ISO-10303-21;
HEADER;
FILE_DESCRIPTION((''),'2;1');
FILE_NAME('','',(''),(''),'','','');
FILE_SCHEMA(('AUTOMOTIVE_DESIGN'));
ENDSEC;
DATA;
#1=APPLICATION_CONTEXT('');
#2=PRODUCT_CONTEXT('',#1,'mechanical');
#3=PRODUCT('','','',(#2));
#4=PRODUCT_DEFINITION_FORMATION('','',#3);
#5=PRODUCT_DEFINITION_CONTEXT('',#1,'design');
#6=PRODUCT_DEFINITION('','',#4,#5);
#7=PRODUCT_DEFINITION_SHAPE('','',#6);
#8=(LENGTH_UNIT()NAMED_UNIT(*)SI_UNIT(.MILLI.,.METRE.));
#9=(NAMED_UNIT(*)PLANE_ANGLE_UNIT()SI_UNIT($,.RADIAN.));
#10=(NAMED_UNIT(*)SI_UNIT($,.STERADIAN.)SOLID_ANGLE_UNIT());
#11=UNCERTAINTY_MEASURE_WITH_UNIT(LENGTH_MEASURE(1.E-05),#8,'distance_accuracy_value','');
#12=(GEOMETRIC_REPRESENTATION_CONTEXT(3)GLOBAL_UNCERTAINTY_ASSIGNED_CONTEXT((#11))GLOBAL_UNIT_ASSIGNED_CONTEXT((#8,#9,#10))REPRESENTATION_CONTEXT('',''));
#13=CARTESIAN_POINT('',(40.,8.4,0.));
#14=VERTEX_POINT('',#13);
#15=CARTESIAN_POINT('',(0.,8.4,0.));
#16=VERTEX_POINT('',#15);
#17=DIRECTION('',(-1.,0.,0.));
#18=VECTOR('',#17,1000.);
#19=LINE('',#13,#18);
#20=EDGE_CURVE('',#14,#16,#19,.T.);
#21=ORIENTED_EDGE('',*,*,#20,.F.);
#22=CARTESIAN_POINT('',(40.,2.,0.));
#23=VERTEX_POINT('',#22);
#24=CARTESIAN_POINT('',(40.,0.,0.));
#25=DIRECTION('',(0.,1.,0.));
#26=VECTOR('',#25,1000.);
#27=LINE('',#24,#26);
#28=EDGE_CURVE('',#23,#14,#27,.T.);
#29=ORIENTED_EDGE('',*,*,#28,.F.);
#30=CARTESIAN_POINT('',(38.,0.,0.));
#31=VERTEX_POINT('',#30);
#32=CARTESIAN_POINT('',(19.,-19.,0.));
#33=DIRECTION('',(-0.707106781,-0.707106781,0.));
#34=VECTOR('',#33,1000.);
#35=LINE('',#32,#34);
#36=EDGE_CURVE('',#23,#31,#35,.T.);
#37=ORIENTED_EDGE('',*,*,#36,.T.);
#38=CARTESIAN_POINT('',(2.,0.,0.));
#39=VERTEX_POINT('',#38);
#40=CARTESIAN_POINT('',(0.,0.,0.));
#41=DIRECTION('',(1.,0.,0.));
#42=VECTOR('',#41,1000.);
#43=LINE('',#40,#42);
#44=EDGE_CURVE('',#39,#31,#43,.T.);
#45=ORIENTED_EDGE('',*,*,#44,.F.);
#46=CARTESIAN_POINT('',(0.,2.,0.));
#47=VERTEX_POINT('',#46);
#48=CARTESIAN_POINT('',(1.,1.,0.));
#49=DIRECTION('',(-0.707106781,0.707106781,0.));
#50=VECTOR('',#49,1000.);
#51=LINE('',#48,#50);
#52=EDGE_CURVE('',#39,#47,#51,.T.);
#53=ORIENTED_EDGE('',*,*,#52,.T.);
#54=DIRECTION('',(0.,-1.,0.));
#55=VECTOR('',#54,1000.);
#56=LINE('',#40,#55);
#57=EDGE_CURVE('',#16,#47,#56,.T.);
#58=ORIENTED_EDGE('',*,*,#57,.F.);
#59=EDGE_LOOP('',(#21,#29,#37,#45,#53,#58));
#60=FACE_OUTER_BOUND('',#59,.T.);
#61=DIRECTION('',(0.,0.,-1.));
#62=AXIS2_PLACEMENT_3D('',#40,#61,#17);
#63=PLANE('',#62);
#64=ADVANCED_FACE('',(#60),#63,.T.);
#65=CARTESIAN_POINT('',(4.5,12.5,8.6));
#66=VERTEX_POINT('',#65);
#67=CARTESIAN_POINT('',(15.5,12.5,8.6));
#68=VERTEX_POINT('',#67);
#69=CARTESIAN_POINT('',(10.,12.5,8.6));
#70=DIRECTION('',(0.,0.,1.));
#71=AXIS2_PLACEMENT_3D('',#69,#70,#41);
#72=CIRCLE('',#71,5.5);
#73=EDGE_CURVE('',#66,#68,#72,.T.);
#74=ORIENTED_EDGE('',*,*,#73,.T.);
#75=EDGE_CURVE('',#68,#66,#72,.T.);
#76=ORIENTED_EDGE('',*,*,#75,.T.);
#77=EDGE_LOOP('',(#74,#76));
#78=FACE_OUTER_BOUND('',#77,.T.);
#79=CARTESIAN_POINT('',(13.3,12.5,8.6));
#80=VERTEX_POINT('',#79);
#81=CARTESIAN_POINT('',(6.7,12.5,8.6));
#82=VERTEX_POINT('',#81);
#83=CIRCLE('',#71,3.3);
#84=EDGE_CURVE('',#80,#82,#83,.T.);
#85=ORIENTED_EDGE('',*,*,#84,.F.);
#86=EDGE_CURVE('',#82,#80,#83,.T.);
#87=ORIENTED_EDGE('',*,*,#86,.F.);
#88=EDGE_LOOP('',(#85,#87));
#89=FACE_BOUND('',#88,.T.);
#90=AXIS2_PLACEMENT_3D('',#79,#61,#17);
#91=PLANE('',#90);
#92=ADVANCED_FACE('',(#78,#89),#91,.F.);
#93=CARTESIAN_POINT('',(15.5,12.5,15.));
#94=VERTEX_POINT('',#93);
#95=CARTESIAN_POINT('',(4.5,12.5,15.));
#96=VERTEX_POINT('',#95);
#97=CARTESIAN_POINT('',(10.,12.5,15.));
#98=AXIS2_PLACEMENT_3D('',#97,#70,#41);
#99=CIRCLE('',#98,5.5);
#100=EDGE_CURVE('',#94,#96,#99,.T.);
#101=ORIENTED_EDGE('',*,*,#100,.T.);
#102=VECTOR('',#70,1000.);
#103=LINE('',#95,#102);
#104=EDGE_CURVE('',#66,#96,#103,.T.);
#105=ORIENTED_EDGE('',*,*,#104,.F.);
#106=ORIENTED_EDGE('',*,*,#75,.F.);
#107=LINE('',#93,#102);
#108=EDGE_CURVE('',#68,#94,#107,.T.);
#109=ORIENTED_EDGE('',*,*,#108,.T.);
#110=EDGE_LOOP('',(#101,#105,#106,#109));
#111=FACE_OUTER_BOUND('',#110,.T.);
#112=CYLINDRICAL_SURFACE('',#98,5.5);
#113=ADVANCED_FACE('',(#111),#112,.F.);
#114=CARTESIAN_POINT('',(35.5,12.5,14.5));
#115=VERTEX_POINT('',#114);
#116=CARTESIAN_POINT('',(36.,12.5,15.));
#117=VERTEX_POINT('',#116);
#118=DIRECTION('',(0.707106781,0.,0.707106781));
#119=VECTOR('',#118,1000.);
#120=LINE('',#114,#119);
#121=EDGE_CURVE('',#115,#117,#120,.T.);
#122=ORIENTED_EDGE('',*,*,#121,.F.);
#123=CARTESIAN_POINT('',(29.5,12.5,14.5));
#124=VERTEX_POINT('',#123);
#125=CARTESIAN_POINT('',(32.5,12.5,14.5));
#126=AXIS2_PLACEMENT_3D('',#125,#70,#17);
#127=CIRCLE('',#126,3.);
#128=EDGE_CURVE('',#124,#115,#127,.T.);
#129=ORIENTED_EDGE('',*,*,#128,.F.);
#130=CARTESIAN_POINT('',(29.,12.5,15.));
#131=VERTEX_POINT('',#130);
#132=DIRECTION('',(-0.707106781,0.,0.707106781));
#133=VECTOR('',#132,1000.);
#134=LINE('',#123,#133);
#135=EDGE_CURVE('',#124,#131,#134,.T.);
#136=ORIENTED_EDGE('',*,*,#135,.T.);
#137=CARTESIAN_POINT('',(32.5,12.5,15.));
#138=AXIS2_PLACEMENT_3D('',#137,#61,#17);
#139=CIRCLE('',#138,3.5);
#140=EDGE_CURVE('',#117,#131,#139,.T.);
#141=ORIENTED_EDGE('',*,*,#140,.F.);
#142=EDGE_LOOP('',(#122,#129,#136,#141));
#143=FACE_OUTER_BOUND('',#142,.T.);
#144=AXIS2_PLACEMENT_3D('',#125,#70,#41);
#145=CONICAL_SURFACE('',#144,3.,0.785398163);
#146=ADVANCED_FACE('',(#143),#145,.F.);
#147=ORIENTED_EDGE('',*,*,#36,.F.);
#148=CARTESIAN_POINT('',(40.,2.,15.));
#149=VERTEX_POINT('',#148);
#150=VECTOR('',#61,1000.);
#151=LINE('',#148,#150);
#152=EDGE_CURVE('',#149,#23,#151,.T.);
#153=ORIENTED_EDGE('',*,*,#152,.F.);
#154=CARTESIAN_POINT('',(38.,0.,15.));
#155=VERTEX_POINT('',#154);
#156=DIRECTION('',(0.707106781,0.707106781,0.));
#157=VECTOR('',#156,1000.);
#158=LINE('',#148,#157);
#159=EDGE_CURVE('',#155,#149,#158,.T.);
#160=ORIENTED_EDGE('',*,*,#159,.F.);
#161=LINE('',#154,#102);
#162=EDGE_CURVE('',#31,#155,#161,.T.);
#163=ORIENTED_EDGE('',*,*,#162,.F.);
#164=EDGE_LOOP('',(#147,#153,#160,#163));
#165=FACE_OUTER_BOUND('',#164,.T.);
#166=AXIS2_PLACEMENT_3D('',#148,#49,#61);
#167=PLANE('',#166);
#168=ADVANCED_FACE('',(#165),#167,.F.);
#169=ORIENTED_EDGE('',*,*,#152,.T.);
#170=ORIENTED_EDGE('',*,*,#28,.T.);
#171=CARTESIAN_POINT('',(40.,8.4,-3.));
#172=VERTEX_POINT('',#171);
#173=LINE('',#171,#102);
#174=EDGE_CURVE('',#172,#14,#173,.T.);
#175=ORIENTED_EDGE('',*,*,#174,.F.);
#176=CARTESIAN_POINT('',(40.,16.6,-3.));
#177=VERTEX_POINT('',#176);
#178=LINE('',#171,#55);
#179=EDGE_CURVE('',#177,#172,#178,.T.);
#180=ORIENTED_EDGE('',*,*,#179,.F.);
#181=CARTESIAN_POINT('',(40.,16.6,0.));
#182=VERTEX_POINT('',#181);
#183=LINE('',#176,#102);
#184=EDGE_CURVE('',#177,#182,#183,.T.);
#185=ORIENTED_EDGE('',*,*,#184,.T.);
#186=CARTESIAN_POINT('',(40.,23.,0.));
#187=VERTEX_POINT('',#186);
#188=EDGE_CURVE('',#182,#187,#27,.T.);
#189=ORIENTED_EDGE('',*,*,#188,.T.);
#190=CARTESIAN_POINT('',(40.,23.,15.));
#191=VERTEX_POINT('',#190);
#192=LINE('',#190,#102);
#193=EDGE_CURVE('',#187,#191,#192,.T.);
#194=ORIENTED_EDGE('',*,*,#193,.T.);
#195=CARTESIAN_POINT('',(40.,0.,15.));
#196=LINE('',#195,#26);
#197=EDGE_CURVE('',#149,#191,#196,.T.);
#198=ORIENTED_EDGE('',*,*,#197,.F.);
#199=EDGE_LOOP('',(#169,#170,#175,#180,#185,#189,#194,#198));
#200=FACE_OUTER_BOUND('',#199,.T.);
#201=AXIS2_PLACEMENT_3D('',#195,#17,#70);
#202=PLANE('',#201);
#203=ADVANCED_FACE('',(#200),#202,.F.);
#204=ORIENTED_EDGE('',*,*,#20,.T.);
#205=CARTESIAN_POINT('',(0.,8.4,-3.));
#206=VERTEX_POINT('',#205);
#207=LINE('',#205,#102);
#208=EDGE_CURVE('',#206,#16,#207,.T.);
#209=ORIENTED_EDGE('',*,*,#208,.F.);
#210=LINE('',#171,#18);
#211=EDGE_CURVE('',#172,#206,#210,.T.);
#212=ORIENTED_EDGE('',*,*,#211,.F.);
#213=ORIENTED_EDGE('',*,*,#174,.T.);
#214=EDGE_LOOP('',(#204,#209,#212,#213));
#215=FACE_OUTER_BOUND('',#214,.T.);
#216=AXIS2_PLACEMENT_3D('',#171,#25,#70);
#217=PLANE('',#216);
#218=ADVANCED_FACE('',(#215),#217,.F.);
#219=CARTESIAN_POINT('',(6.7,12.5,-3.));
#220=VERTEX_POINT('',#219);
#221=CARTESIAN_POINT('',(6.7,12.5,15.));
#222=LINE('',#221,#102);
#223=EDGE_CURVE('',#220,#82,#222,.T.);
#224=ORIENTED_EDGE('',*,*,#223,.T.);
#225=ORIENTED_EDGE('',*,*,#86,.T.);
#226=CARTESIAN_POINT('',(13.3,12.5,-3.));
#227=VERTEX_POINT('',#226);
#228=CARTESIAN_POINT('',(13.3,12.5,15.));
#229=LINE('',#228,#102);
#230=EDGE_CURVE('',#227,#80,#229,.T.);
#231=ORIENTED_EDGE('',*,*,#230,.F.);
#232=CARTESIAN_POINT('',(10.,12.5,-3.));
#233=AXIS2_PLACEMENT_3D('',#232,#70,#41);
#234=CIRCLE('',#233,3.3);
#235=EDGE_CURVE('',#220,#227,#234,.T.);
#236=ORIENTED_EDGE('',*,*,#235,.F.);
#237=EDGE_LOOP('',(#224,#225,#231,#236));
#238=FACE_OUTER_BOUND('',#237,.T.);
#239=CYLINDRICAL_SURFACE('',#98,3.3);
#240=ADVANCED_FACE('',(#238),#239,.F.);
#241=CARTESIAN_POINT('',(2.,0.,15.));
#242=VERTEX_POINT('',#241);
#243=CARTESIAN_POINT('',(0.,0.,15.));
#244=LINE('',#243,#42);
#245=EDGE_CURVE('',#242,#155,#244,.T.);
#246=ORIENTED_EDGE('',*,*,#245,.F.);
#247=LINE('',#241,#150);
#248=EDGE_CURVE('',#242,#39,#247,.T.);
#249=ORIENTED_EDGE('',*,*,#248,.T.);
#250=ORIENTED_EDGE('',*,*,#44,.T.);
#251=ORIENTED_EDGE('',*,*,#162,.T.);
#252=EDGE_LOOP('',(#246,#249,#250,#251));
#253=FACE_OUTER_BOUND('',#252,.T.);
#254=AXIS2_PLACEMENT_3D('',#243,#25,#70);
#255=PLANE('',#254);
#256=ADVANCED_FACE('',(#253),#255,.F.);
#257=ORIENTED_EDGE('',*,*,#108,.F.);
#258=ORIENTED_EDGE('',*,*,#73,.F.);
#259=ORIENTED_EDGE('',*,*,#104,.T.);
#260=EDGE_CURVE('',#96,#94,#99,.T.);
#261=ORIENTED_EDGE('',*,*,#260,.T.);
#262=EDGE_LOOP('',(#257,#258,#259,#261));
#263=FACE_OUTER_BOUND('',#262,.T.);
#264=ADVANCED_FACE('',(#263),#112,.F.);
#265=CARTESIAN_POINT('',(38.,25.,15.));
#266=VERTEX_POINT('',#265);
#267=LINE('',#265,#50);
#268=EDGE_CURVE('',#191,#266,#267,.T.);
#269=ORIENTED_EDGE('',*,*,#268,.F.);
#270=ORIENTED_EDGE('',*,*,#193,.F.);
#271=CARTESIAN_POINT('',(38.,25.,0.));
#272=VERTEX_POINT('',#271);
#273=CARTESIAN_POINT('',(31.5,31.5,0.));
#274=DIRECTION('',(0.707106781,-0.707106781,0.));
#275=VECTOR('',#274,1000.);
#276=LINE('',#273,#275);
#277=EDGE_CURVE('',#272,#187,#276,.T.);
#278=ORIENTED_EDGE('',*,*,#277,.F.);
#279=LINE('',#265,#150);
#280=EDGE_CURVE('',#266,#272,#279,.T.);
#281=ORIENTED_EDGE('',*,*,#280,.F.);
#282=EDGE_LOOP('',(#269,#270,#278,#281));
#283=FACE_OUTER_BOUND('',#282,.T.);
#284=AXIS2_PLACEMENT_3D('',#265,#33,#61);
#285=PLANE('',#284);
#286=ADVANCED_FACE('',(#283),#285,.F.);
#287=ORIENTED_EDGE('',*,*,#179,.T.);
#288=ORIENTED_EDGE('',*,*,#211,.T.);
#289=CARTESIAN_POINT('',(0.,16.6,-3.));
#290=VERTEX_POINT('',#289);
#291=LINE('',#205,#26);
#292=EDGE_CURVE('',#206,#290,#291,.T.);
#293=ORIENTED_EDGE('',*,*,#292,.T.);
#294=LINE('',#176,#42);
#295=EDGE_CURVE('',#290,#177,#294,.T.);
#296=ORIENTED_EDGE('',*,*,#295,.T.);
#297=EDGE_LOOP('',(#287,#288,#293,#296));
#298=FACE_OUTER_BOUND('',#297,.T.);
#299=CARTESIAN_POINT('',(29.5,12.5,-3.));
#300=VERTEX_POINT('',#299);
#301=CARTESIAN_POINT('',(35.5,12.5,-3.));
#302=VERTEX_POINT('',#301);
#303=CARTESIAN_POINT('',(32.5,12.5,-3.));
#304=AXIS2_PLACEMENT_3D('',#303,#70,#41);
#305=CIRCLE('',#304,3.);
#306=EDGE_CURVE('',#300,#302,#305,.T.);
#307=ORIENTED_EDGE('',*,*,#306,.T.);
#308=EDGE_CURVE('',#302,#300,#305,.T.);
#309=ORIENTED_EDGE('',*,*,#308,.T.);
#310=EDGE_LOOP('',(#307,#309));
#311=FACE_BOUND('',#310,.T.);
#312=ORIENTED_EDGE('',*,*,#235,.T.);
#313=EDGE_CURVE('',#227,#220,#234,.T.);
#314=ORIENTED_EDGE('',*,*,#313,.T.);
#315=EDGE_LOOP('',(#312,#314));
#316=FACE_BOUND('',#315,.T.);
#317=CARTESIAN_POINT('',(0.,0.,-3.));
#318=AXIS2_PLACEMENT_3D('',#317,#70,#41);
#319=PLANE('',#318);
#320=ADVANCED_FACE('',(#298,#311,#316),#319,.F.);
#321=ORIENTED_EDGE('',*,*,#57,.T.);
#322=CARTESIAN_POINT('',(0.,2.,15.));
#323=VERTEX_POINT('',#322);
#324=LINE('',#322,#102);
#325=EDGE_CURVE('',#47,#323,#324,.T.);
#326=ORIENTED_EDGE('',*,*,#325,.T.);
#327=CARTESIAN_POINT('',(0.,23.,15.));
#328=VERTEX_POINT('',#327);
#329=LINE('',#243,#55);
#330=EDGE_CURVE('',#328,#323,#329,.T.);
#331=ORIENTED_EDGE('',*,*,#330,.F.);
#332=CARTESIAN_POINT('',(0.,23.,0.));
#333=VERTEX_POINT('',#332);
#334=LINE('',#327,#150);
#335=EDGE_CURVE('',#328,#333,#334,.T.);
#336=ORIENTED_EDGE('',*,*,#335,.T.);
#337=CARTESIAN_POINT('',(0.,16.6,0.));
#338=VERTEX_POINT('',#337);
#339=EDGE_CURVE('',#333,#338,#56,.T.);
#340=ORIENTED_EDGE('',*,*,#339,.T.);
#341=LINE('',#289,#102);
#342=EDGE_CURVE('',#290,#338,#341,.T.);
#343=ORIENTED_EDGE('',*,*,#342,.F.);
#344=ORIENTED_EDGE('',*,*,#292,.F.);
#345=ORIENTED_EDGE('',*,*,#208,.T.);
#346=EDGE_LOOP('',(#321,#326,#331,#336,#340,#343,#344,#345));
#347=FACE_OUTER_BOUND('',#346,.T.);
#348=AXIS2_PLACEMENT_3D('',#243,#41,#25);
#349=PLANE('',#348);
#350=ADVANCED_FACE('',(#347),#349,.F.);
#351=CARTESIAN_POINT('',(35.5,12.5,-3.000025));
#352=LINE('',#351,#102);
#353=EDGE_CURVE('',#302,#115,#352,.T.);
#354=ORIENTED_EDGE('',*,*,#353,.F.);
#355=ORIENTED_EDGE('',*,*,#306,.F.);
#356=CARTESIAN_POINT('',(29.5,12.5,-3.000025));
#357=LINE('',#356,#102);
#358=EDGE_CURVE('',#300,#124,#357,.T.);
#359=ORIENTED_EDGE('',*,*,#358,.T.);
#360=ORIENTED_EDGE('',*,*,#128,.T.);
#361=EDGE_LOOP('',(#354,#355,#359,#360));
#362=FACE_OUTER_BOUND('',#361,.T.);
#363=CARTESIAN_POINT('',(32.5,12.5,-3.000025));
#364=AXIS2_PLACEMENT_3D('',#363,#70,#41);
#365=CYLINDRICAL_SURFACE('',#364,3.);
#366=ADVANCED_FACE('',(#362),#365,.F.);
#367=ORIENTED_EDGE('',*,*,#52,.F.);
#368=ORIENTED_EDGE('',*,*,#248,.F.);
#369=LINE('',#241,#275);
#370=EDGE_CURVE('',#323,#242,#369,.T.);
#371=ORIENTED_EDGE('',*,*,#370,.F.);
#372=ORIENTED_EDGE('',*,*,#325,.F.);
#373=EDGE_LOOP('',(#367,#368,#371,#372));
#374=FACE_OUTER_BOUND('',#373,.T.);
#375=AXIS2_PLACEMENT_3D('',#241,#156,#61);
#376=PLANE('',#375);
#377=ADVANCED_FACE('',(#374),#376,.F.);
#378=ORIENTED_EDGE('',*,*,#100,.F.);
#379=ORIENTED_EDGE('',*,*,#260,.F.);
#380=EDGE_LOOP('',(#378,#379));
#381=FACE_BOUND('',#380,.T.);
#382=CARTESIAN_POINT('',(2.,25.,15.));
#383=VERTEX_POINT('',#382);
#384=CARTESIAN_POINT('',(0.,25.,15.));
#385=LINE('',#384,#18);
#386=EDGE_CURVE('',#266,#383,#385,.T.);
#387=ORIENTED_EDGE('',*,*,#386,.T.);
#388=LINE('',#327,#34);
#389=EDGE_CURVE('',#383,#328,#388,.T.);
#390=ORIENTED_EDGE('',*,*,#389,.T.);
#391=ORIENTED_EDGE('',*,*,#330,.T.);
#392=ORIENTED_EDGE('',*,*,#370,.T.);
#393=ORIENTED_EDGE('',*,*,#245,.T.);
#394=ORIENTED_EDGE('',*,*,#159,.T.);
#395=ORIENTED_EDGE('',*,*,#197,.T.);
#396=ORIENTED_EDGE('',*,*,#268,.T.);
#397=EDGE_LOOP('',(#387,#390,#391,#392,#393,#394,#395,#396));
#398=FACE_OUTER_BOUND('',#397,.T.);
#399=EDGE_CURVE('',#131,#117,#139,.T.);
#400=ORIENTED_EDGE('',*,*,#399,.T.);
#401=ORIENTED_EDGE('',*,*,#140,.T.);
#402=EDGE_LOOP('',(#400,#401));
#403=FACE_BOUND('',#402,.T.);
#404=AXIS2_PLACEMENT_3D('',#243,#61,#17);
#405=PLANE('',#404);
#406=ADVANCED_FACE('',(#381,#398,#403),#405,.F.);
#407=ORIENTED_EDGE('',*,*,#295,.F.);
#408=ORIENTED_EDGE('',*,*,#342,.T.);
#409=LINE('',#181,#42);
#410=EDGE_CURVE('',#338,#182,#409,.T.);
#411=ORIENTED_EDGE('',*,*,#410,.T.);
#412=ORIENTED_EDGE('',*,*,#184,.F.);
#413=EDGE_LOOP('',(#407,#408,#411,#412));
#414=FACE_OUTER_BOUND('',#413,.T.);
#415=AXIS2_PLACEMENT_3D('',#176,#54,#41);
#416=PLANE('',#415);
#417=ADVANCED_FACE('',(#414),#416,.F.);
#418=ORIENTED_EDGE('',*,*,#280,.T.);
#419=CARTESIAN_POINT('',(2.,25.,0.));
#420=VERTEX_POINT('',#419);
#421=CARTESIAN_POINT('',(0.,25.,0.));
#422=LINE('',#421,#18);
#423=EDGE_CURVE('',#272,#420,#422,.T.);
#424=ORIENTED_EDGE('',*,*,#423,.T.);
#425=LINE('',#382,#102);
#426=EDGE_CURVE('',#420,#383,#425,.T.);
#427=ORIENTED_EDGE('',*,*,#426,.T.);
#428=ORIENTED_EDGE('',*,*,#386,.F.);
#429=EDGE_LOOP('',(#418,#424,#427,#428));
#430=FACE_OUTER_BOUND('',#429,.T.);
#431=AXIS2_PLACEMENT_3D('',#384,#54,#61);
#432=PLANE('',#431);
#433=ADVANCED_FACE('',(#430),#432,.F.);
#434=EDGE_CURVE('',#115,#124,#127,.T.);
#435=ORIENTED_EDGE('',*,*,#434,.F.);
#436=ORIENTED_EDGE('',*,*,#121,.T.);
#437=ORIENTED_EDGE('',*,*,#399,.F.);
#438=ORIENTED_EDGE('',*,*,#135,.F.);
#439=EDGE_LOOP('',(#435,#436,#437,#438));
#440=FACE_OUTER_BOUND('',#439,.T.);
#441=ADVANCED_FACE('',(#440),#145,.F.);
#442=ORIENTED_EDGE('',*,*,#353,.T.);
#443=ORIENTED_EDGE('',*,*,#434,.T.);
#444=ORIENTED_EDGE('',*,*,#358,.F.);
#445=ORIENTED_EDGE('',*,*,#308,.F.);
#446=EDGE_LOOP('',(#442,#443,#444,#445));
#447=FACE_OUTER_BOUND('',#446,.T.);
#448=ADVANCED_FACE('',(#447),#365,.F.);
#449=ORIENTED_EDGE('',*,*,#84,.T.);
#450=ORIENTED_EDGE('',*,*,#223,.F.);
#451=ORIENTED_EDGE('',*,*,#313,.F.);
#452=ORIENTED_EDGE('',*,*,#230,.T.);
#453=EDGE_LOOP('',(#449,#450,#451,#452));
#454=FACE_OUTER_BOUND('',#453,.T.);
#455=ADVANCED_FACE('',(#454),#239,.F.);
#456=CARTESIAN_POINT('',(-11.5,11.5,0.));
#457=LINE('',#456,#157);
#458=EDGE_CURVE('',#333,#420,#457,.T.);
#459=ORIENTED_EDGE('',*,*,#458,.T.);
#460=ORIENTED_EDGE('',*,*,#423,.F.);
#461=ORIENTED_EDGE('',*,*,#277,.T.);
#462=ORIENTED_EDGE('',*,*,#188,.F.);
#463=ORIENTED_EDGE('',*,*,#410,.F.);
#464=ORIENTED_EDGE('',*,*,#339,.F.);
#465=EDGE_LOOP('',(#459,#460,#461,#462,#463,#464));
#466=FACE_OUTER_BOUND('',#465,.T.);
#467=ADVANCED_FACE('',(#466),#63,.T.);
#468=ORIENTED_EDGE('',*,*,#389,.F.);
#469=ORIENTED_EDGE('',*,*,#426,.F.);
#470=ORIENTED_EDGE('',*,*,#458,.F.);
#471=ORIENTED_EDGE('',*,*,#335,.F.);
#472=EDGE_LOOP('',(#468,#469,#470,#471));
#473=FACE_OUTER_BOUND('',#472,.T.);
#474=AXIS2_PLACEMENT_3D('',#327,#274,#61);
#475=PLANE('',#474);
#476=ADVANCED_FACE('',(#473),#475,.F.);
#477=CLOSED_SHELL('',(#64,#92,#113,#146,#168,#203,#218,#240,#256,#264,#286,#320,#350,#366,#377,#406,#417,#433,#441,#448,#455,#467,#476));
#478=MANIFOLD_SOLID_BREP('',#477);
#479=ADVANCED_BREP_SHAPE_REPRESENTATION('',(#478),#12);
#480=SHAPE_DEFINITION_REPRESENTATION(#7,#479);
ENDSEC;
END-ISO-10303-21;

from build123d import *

# Parameters (mm, degrees)
SKETCH_1_W                   = 40
SKETCH_1_H                   = 25
EXTRUDE_1_DEPTH              = 15
SKETCH_9_W                   = 40
SKETCH_9_H                   = 8.2
EXTRUDE_3_DEPTH              = 3
HOLE_WIZARD_M6_2_D           = 6.6
HOLE_WIZARD_M6_2_CBORE_D     = 11
HOLE_WIZARD_M6_2_CBORE_DEPTH = 6.4
SKETCH_12_R                  = 3
CUT_EXTRUDE_3_DEPTH          = 51.487622245
CHAMFER_2_SIZE               = 0.5
CHAMFER_3_SIZE               = 2


with BuildPart() as part:
    # 草图1 → 凸台-拉伸1 (new body)
    with BuildSketch(Plane.XY):
        with Locations((20, 12.5)):
            Rectangle(SKETCH_1_W, SKETCH_1_H)
    extrude(amount=EXTRUDE_1_DEPTH)

    # 草图9 → 凸台-拉伸3 (add)
    with BuildSketch(Plane(origin=(0, 0, 0), x_dir=(-1, 0, 0), z_dir=(0, 0, -1))):
        with Locations((-20, 12.5)):
            Rectangle(SKETCH_9_W, SKETCH_9_H)
    extrude(amount=EXTRUDE_3_DEPTH)

    # M6 六角凹头螺钉的柱形沉头孔2 (through all)
    with Locations(Plane.XY.offset(15)):
        with Locations((10, 12.5)):
            CounterBoreHole(HOLE_WIZARD_M6_2_D / 2, HOLE_WIZARD_M6_2_CBORE_D / 2, HOLE_WIZARD_M6_2_CBORE_DEPTH)

    # 草图12 → 切除-拉伸3 (cut, through all)
    with BuildSketch(Plane.XY.offset(15)):
        with Locations((32.5, 12.5)):
            Circle(SKETCH_12_R)
    extrude(amount=-CUT_EXTRUDE_3_DEPTH, mode=Mode.SUBTRACT)

    # 倒角2
    chamfer_2_edges = [part.edges().sort_by_distance(p)[0] for p in [
        (29.5, 12.5, 15),
    ]]
    chamfer(chamfer_2_edges, length=CHAMFER_2_SIZE)

    # 倒角3
    chamfer_3_edges = [part.edges().sort_by_distance(p)[0] for p in [
        (40, 0, 7.5),
        (0, 0, 7.5),
        (0, 25, 7.5),
        (40, 25, 7.5),
    ]]
    chamfer(chamfer_3_edges, length=CHAMFER_3_SIZE)


solid = part.part
